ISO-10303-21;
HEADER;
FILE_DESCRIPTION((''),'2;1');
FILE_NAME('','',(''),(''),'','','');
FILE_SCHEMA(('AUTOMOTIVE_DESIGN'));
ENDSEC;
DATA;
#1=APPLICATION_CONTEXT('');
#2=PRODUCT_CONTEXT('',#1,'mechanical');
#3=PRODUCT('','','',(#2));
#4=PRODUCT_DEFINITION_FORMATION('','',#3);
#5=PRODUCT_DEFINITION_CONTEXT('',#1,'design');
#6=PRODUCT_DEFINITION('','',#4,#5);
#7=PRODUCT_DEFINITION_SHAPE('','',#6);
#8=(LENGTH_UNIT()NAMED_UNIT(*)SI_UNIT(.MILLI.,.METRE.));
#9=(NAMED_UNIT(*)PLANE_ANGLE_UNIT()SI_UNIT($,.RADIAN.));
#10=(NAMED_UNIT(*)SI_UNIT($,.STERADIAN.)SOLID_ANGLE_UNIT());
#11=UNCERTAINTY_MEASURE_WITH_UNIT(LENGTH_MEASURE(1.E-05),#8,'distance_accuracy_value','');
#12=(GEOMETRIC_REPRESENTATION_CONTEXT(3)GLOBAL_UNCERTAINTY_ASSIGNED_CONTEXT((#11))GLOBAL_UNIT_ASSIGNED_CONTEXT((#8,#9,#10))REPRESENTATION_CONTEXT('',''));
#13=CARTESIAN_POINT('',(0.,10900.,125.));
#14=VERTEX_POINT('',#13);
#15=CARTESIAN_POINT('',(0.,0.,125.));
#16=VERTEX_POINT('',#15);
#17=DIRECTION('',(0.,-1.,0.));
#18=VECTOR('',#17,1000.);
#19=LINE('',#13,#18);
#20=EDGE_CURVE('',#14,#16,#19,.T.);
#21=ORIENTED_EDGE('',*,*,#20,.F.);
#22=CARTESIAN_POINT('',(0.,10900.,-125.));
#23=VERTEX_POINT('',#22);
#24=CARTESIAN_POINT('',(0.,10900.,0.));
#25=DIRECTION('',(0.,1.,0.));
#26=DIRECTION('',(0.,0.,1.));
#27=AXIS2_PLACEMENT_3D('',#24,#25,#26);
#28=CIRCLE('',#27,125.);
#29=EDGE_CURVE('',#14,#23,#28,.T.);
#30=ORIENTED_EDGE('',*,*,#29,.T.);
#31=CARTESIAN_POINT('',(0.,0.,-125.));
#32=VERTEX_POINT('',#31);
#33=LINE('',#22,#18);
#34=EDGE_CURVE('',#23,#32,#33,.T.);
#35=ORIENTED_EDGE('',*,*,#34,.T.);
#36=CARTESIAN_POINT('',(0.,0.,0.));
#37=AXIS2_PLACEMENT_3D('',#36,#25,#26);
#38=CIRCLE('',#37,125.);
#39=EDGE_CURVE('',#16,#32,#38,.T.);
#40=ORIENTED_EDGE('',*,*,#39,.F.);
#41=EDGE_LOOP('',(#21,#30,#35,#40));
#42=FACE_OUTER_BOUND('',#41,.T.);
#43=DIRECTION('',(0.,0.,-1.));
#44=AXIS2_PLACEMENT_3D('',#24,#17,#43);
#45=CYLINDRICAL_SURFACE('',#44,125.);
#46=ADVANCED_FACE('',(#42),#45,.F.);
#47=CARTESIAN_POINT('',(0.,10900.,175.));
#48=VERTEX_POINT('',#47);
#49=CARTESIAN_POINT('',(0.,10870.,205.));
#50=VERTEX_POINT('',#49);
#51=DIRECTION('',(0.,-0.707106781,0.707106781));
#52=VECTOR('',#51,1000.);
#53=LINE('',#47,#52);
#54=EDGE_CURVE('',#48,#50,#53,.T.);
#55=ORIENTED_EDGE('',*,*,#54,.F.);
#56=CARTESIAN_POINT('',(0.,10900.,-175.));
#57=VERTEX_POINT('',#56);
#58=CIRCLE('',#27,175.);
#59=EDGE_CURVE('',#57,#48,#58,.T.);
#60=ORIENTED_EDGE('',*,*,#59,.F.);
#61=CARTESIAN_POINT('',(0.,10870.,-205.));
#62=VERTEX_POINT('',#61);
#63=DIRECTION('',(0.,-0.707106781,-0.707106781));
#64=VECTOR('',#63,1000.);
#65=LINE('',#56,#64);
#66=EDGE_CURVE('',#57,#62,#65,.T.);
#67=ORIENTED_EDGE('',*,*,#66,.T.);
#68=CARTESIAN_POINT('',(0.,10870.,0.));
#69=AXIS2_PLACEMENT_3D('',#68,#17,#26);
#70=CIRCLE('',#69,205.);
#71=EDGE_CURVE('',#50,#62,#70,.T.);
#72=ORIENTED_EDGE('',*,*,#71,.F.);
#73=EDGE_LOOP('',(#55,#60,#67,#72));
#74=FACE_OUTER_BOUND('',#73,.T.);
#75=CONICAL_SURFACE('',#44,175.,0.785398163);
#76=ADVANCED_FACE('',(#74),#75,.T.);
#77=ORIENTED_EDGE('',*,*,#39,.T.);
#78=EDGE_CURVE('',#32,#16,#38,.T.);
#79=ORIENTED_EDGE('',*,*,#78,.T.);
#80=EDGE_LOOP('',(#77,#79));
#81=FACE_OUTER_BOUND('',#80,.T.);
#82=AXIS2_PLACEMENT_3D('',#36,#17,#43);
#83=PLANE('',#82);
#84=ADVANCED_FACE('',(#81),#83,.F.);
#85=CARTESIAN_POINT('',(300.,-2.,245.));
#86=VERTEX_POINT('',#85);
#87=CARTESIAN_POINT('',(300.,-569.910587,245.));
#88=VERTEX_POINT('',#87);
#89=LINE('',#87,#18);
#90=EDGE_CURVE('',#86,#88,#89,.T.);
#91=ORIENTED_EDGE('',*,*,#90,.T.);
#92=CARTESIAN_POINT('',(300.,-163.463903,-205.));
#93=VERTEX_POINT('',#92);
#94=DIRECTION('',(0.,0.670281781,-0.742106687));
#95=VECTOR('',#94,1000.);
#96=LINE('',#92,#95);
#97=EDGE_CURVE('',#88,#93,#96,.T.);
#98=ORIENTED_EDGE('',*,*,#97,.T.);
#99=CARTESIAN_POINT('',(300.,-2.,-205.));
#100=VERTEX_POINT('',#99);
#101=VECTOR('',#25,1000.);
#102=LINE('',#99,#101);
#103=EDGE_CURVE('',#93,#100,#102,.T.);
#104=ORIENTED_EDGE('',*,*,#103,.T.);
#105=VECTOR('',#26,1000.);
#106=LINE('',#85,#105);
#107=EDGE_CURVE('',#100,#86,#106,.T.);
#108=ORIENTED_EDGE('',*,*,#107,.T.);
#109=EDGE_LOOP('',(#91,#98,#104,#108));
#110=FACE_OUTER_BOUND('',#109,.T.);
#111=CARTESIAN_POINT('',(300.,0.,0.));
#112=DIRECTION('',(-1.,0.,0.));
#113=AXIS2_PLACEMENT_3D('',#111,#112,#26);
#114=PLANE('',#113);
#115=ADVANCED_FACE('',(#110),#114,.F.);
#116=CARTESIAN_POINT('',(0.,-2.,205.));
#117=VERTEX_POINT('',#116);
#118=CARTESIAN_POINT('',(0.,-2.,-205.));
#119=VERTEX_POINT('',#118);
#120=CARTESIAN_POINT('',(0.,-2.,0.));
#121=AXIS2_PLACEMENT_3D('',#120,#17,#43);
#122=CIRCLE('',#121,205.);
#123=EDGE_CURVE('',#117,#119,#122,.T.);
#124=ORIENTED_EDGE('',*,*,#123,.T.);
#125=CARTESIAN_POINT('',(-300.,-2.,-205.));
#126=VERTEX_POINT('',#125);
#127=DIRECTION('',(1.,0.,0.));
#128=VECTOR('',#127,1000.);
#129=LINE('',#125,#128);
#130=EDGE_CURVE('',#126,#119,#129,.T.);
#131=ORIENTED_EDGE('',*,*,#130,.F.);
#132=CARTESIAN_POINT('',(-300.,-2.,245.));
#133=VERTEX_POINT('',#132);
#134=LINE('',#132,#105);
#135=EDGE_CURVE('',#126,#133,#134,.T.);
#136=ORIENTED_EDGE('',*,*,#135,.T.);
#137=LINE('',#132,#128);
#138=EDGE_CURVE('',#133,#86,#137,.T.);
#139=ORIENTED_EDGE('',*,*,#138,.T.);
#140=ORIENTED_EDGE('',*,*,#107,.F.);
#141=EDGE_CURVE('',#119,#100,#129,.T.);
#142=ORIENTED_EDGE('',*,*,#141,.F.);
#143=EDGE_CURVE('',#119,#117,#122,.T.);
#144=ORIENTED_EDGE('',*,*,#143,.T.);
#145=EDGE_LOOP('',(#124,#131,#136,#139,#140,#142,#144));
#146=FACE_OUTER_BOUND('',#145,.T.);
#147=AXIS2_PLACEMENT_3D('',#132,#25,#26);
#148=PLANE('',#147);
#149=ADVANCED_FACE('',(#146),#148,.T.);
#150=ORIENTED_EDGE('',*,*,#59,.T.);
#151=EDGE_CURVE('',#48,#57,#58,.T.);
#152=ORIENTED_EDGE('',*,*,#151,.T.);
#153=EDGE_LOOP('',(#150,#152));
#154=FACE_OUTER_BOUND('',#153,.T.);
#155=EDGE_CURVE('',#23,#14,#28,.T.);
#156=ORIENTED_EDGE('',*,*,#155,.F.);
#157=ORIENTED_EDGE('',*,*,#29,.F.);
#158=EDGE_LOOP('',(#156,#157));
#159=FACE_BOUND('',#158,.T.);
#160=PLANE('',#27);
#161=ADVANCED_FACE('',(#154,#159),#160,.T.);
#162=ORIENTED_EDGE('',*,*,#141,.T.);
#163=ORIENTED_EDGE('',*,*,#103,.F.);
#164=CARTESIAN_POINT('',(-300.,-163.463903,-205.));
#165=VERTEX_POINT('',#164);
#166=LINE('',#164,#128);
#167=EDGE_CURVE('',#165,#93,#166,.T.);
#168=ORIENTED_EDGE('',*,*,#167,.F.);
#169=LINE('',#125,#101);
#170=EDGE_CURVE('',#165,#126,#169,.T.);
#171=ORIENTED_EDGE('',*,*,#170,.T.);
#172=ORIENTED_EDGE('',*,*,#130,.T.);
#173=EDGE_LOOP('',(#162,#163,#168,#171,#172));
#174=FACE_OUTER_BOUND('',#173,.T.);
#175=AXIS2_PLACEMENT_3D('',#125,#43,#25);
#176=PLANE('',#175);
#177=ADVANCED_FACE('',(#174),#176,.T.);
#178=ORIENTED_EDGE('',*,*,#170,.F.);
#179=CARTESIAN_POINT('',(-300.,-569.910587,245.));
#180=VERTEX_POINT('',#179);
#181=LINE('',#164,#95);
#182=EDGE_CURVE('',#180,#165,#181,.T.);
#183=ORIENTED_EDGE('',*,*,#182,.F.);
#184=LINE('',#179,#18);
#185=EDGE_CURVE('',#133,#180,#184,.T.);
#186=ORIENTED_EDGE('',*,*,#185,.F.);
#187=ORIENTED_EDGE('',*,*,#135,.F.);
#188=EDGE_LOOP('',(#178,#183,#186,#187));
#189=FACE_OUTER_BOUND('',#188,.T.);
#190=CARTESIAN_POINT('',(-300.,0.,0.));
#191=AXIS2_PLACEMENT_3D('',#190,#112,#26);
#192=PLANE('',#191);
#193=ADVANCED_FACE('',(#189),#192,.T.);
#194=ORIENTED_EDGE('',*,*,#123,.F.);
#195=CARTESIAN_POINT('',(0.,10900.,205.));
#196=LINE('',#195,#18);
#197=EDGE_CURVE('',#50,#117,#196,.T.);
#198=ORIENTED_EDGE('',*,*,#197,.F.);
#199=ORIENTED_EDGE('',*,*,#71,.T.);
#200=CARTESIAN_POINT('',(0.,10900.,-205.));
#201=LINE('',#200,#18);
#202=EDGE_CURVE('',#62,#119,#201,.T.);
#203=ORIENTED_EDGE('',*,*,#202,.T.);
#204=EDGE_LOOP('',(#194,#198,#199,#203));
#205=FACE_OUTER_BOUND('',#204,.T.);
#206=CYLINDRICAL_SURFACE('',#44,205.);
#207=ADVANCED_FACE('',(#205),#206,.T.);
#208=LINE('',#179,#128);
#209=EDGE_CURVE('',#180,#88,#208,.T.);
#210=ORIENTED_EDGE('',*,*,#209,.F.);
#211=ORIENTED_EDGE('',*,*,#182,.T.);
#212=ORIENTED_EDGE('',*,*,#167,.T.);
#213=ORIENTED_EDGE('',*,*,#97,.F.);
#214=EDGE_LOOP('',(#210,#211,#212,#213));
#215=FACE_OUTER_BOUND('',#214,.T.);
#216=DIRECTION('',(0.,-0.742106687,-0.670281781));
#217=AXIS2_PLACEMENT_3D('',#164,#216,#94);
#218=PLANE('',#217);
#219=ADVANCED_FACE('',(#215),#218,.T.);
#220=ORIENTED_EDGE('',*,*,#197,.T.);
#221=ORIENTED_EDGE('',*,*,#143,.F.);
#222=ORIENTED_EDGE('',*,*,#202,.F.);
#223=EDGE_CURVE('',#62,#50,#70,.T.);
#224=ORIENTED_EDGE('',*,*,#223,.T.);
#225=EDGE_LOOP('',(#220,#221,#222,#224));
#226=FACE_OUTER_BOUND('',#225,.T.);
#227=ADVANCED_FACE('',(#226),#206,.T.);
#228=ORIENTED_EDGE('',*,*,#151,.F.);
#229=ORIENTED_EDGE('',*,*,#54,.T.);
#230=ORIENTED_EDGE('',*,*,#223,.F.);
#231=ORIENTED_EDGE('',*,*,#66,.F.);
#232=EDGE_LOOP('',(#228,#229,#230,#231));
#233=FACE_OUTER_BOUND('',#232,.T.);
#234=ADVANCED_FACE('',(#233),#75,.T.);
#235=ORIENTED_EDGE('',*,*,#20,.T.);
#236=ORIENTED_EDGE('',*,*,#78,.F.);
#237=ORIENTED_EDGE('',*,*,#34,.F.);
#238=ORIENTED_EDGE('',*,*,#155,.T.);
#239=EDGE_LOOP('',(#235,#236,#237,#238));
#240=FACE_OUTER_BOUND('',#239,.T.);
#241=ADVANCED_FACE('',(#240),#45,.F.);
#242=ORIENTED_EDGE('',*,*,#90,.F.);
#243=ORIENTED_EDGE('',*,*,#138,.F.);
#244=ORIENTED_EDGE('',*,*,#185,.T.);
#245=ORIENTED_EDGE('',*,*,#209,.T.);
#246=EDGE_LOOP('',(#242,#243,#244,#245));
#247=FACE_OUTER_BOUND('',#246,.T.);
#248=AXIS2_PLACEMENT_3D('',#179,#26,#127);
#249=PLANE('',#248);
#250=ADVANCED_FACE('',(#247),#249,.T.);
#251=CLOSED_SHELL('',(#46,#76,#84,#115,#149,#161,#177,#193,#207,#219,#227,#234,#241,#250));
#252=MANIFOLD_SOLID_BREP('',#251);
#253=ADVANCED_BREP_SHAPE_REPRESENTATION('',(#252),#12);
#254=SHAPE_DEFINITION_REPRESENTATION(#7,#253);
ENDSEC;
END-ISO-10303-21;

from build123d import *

# Parameters (mm, degrees)
SKETCH1_R                = 205
SKETCH1_R_2              = 125
BOSS_EXTRUDE1_DEPTH      = 10900
BOSS_EXTRUDE2_START      = 2
SKETCH2_R                = 205
BOSS_EXTRUDE2_DEPTH      = 2
CHAMFER1_SIZE            = 30
BOSS_EXTRUDE3_DEPTH      = 300
BOSS_EXTRUDE3_DEPTH_BACK = 300


with BuildPart() as part:
    # Sketch1 → Boss-Extrude1 (new body)
    with BuildSketch(Plane(origin=(0, 0, 0), x_dir=(1, 0, 0), z_dir=(0, 1, 0))):
        with Locations(Location((0, 0, 0), (0, 0, 90))):
            Circle(SKETCH1_R)
        with Locations(Location((0, 0, 0), (0, 0, 90))):
            Circle(SKETCH1_R_2, mode=Mode.SUBTRACT)
    extrude(amount=BOSS_EXTRUDE1_DEPTH)

    # Sketch2 → Boss-Extrude2 (add)
    with BuildSketch(Plane.XZ.offset(BOSS_EXTRUDE2_START)):
        with Locations(Location((0, 0, 0), (0, 0, 270))):
            Circle(SKETCH2_R)
    extrude(amount=-BOSS_EXTRUDE2_DEPTH)

    # Chamfer1
    chamfer1_edges = [part.edges().sort_by_distance(p)[0] for p in [
        (0, 10900, 205),
    ]]
    chamfer(chamfer1_edges, length=CHAMFER1_SIZE)

    # Sketch3 → Boss-Extrude3 (add, two sides: drawn at the far end of the back side and taken through both)
    with BuildSketch(Plane(origin=(0, 0, 0), x_dir=(0, 0, -1), z_dir=(1, 0, 0)).offset(-BOSS_EXTRUDE3_DEPTH_BACK)):
        Polygon((205, -2), (205, -163.463903414), (-245, -569.910586712), (-245, -2), align=None)
    extrude(amount=BOSS_EXTRUDE3_DEPTH + BOSS_EXTRUDE3_DEPTH_BACK)


solid = part.part
